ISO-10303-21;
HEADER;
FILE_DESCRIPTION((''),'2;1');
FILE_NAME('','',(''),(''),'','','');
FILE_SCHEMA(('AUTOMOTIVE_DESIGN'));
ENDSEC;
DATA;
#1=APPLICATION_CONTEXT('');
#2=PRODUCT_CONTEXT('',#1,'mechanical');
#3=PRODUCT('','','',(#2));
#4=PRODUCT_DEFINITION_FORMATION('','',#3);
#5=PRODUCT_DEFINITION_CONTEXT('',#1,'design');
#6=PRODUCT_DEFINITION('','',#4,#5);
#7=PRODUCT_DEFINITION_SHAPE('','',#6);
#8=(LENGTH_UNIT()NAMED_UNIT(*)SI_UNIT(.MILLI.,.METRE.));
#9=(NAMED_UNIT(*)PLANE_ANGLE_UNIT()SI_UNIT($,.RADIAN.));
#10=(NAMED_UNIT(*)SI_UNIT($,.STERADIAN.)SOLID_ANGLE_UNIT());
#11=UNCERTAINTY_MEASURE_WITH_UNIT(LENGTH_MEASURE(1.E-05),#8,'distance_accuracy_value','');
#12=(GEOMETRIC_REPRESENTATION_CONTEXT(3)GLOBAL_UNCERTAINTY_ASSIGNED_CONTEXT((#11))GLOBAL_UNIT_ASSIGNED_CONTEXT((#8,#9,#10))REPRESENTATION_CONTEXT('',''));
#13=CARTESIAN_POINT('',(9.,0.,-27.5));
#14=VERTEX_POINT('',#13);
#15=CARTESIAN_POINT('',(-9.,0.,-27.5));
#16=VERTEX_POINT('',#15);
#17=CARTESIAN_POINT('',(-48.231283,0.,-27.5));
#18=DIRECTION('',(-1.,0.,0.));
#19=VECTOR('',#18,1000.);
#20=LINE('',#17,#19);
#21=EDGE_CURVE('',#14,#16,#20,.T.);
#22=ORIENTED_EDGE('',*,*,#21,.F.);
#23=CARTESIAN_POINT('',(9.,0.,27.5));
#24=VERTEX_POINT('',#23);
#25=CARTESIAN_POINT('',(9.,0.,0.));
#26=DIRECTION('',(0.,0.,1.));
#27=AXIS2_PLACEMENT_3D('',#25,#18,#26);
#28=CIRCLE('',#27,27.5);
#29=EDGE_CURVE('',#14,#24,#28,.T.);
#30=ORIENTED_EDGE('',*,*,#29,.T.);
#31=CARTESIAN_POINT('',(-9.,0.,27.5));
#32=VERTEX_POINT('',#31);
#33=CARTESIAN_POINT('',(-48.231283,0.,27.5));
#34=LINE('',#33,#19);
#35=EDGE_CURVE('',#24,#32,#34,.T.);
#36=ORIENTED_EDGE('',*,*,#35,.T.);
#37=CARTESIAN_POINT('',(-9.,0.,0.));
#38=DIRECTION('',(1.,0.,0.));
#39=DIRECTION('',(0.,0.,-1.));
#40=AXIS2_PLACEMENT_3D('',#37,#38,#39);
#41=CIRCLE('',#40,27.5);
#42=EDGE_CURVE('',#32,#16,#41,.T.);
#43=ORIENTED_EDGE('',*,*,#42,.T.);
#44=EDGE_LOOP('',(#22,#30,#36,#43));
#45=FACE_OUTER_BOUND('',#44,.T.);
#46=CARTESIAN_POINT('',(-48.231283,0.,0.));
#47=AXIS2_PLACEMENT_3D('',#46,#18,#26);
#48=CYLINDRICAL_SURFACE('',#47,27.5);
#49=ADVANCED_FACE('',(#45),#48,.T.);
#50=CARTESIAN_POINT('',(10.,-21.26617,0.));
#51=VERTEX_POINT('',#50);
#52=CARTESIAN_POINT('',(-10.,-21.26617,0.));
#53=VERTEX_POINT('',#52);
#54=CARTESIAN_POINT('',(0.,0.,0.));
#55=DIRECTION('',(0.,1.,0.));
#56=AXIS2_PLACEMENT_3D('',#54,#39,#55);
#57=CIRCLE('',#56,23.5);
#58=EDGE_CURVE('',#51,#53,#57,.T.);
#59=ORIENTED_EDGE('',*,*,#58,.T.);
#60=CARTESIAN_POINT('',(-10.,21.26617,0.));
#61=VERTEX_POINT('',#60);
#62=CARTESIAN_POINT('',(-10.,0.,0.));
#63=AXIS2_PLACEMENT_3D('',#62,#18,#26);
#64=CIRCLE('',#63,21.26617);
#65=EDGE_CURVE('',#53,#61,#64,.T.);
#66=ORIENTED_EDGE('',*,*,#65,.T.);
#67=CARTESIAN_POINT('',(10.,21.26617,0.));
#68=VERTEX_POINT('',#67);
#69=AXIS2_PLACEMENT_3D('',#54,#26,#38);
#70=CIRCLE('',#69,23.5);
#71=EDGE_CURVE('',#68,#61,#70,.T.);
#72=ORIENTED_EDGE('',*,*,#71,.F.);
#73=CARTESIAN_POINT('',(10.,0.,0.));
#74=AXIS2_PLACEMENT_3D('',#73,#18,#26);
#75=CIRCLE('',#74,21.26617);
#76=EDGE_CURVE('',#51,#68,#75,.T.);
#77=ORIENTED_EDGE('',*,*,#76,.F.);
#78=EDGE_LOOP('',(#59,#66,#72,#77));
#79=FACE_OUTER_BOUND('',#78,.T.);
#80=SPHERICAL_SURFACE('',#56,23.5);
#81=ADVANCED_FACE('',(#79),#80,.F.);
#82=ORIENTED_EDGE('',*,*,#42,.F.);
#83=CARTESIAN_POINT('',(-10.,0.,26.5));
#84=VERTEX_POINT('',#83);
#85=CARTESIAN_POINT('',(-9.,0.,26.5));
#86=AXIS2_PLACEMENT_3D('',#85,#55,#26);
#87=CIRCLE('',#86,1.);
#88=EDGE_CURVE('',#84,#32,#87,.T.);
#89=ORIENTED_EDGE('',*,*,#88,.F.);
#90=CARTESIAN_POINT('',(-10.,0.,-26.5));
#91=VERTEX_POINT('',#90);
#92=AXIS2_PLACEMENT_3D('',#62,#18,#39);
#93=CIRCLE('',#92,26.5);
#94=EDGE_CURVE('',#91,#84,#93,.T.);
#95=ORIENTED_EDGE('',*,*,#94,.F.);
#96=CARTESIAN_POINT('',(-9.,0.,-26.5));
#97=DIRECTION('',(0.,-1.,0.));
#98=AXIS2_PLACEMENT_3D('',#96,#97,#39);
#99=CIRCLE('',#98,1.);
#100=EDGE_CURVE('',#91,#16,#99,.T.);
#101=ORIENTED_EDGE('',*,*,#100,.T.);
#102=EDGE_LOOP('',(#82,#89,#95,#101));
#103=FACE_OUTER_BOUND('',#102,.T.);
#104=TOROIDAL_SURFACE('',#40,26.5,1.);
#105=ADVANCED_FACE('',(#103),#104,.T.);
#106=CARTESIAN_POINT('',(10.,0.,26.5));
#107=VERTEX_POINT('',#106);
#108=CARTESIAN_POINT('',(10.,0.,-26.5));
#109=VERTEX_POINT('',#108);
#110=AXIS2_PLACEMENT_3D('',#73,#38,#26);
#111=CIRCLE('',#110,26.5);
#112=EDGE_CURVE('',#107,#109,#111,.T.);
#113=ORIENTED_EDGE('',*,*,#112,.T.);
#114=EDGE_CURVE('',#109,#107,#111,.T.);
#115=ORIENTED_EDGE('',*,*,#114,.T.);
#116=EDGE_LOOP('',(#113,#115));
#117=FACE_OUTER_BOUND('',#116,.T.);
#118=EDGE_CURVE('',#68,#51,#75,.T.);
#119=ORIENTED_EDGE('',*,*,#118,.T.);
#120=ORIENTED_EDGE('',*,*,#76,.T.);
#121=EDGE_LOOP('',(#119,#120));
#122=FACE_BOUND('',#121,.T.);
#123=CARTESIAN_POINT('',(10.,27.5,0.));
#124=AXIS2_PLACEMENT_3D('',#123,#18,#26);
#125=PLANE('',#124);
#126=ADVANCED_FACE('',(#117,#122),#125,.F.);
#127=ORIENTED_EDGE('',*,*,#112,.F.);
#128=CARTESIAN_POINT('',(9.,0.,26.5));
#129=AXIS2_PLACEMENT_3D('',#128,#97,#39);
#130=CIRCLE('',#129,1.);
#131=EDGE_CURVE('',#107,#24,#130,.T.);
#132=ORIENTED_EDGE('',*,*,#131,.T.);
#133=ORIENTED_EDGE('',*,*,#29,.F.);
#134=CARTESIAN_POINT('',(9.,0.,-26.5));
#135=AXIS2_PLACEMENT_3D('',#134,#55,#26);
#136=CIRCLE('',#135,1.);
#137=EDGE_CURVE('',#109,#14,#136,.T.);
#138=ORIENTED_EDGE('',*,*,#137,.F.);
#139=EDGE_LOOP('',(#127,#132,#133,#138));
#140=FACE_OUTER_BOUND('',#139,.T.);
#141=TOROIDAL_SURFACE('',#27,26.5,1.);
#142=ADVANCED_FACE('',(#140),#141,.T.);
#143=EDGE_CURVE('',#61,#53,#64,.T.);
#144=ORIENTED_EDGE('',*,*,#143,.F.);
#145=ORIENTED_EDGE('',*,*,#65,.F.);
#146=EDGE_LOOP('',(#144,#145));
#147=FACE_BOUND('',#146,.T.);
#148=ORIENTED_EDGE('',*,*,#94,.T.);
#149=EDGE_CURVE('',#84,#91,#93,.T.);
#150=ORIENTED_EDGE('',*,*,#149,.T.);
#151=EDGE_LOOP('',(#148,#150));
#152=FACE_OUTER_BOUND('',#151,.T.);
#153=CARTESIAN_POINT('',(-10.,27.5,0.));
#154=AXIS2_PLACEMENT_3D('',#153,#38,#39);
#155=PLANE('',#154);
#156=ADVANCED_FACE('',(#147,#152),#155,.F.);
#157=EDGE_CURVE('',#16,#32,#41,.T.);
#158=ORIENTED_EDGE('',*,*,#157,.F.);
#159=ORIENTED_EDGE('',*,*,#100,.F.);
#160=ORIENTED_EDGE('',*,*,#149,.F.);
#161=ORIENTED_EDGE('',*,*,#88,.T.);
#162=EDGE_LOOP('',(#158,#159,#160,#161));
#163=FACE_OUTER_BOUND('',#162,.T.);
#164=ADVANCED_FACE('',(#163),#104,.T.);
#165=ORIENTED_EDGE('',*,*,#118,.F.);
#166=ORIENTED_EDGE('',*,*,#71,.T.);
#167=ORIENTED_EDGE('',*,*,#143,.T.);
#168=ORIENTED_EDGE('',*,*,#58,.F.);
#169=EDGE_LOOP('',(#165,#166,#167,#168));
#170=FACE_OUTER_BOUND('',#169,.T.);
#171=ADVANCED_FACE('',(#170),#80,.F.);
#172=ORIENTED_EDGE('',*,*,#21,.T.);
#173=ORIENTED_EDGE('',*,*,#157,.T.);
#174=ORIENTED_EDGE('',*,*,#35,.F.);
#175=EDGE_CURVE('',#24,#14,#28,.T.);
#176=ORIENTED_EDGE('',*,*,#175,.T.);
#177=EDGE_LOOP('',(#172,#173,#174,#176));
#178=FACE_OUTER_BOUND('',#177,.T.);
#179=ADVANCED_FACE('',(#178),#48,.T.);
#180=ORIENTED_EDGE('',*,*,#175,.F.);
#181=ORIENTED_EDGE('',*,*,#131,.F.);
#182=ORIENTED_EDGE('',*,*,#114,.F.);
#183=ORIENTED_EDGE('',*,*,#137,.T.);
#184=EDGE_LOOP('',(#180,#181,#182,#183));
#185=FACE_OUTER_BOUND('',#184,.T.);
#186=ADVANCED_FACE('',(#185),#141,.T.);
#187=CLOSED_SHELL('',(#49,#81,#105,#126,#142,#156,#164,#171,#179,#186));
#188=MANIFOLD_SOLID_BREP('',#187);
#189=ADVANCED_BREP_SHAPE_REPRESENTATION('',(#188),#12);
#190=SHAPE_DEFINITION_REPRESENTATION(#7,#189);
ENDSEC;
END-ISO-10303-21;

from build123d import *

# Parameters (mm, degrees)
FILLET_1_R = 1


with BuildPart() as part:
    # 草图1 → 旋转1 (revolve)
    with BuildSketch(Plane.XY, mode=Mode.PRIVATE) as revolve_1_sk:
        with BuildLine():
            Line((-10, 27.5), (-10, 21.266170318))
            ThreePointArc((-10, 21.266170318), (0, 23.5), (10, 21.266170318))
            Line((10, 21.266170318), (10, 27.5))
            Line((10, 27.5), (-10, 27.5))
        make_face()
    revolve(revolve_1_sk.sketch.rotate(Axis((-48.231282768, 0, 0), (1, 0, 0)), 90), axis=Axis((-48.231282768, 0, 0), (1, 0, 0)))

    # 圆角1
    fillet_1_edges = [part.edges().sort_by_distance(p)[0] for p in [
        (10, 0, -27.5),
        (-10, 0, -27.5),
    ]]
    fillet(fillet_1_edges, radius=FILLET_1_R)


solid = part.part
